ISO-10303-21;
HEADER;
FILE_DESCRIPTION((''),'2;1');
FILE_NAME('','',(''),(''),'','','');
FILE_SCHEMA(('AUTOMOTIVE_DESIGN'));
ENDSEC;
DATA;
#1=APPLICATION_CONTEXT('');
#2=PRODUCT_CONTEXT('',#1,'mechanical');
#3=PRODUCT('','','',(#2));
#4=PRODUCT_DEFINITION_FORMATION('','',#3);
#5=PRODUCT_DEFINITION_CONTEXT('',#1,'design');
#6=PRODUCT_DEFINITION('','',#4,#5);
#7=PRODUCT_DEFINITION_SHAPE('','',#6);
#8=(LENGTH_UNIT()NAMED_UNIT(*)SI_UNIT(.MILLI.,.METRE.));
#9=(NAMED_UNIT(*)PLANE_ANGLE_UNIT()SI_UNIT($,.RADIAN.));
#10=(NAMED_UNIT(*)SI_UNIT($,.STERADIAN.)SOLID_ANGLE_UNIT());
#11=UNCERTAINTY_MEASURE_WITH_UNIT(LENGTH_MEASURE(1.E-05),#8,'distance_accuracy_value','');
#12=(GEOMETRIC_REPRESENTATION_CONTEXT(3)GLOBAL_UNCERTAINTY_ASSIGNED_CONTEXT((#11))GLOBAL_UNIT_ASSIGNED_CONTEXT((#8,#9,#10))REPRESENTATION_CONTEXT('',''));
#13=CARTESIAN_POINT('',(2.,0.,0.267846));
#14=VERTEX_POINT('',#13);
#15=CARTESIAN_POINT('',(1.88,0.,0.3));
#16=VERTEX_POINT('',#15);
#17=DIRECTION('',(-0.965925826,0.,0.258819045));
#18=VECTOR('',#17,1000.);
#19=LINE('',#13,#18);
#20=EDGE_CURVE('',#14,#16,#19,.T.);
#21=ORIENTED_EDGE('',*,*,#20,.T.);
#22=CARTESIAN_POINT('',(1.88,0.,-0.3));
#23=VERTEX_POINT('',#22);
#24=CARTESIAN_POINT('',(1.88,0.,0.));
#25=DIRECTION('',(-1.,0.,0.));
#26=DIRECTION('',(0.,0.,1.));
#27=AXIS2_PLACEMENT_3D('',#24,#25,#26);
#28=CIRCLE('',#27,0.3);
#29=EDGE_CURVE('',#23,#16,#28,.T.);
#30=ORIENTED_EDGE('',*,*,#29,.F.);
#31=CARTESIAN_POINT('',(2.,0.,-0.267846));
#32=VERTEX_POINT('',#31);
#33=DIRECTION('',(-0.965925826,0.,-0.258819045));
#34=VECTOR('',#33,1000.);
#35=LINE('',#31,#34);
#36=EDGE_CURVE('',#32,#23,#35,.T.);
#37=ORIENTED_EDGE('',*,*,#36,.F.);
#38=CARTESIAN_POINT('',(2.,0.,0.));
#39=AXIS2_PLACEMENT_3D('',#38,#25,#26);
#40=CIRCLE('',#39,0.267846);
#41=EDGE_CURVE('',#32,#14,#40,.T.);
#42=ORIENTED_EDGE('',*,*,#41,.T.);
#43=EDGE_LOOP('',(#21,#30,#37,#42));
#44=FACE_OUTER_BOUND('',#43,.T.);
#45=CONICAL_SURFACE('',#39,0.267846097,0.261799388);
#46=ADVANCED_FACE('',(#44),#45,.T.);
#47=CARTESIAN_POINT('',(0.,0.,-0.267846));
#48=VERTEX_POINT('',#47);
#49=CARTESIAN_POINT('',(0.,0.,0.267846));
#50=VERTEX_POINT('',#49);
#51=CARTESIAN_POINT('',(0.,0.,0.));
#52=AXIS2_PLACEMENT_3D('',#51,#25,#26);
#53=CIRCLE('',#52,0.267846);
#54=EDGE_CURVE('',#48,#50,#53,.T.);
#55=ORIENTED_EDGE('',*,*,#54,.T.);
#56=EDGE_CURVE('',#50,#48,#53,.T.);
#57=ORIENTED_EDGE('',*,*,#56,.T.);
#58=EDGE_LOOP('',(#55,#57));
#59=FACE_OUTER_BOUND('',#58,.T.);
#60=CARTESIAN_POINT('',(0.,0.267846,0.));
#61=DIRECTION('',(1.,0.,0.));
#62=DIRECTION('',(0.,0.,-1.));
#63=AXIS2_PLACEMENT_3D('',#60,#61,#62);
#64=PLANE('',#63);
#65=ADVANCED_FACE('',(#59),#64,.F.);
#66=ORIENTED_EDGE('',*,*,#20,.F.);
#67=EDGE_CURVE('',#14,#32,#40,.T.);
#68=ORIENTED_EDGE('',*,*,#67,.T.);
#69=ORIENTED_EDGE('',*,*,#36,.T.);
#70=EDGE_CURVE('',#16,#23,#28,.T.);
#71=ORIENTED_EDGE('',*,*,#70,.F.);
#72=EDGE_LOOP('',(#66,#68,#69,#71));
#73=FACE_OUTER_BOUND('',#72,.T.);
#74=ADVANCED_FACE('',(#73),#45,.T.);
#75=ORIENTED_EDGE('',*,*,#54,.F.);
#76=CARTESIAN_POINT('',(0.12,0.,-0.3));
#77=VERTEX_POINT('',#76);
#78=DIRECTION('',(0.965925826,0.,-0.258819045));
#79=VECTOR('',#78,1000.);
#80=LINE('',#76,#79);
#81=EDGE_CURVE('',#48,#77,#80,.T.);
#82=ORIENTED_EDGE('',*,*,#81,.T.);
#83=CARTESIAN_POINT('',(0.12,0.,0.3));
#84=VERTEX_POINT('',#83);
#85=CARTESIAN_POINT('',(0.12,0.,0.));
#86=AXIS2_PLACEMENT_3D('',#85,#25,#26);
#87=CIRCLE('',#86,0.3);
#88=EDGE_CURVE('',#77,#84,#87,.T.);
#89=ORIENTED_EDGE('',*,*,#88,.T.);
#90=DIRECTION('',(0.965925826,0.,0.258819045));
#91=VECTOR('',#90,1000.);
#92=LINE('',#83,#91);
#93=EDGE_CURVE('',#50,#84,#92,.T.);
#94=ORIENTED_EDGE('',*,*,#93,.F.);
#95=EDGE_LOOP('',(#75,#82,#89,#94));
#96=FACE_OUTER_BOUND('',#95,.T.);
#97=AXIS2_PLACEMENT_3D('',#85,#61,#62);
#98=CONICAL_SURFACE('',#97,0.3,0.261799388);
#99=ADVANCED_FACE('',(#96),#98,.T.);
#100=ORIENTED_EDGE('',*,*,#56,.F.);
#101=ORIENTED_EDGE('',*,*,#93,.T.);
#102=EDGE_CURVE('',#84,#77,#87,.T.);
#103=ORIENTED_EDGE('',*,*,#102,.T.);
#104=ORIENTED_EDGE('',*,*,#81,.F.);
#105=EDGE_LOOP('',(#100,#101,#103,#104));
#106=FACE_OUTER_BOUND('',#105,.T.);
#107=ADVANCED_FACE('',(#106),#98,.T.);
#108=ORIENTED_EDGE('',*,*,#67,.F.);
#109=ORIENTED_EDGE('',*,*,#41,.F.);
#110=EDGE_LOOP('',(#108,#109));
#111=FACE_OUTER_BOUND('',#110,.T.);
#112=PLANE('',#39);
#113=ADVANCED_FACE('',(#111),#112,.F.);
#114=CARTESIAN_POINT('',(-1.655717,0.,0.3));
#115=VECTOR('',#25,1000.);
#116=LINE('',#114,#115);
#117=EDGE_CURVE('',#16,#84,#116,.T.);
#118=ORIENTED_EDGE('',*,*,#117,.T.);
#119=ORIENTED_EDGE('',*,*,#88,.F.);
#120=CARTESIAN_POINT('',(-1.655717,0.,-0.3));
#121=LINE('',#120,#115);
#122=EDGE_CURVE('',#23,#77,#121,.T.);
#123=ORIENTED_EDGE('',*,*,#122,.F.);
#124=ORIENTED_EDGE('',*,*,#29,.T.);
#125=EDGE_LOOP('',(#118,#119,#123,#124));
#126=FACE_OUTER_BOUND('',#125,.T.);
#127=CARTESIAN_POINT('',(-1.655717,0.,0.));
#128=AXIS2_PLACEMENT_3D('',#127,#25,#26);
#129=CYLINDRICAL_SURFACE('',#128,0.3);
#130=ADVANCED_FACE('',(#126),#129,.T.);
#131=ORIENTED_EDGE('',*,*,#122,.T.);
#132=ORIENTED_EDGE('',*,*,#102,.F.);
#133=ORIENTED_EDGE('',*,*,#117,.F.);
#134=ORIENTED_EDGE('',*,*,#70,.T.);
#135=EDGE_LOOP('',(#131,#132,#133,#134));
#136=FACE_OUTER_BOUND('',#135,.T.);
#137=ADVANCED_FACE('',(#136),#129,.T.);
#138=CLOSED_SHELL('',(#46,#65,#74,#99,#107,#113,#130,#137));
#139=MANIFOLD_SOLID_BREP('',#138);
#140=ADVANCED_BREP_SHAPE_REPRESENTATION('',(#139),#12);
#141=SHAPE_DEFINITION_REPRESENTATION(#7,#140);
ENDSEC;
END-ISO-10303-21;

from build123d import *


with BuildPart() as part:
    # Sketch1 → Base-Revolve (revolve)
    with BuildSketch(Plane.XY, mode=Mode.PRIVATE) as base_revolve_sk:
        Polygon((0, 0), (2, 0), (2, 0.267846097), (1.88, 0.3), (0.12, 0.3), (0, 0.267846097), align=None)
    revolve(base_revolve_sk.sketch.rotate(Axis((-1.655717266, 0, 0), (1, 0, 0)), 90), axis=Axis((-1.655717266, 0, 0), (1, 0, 0)))


solid = part.part
